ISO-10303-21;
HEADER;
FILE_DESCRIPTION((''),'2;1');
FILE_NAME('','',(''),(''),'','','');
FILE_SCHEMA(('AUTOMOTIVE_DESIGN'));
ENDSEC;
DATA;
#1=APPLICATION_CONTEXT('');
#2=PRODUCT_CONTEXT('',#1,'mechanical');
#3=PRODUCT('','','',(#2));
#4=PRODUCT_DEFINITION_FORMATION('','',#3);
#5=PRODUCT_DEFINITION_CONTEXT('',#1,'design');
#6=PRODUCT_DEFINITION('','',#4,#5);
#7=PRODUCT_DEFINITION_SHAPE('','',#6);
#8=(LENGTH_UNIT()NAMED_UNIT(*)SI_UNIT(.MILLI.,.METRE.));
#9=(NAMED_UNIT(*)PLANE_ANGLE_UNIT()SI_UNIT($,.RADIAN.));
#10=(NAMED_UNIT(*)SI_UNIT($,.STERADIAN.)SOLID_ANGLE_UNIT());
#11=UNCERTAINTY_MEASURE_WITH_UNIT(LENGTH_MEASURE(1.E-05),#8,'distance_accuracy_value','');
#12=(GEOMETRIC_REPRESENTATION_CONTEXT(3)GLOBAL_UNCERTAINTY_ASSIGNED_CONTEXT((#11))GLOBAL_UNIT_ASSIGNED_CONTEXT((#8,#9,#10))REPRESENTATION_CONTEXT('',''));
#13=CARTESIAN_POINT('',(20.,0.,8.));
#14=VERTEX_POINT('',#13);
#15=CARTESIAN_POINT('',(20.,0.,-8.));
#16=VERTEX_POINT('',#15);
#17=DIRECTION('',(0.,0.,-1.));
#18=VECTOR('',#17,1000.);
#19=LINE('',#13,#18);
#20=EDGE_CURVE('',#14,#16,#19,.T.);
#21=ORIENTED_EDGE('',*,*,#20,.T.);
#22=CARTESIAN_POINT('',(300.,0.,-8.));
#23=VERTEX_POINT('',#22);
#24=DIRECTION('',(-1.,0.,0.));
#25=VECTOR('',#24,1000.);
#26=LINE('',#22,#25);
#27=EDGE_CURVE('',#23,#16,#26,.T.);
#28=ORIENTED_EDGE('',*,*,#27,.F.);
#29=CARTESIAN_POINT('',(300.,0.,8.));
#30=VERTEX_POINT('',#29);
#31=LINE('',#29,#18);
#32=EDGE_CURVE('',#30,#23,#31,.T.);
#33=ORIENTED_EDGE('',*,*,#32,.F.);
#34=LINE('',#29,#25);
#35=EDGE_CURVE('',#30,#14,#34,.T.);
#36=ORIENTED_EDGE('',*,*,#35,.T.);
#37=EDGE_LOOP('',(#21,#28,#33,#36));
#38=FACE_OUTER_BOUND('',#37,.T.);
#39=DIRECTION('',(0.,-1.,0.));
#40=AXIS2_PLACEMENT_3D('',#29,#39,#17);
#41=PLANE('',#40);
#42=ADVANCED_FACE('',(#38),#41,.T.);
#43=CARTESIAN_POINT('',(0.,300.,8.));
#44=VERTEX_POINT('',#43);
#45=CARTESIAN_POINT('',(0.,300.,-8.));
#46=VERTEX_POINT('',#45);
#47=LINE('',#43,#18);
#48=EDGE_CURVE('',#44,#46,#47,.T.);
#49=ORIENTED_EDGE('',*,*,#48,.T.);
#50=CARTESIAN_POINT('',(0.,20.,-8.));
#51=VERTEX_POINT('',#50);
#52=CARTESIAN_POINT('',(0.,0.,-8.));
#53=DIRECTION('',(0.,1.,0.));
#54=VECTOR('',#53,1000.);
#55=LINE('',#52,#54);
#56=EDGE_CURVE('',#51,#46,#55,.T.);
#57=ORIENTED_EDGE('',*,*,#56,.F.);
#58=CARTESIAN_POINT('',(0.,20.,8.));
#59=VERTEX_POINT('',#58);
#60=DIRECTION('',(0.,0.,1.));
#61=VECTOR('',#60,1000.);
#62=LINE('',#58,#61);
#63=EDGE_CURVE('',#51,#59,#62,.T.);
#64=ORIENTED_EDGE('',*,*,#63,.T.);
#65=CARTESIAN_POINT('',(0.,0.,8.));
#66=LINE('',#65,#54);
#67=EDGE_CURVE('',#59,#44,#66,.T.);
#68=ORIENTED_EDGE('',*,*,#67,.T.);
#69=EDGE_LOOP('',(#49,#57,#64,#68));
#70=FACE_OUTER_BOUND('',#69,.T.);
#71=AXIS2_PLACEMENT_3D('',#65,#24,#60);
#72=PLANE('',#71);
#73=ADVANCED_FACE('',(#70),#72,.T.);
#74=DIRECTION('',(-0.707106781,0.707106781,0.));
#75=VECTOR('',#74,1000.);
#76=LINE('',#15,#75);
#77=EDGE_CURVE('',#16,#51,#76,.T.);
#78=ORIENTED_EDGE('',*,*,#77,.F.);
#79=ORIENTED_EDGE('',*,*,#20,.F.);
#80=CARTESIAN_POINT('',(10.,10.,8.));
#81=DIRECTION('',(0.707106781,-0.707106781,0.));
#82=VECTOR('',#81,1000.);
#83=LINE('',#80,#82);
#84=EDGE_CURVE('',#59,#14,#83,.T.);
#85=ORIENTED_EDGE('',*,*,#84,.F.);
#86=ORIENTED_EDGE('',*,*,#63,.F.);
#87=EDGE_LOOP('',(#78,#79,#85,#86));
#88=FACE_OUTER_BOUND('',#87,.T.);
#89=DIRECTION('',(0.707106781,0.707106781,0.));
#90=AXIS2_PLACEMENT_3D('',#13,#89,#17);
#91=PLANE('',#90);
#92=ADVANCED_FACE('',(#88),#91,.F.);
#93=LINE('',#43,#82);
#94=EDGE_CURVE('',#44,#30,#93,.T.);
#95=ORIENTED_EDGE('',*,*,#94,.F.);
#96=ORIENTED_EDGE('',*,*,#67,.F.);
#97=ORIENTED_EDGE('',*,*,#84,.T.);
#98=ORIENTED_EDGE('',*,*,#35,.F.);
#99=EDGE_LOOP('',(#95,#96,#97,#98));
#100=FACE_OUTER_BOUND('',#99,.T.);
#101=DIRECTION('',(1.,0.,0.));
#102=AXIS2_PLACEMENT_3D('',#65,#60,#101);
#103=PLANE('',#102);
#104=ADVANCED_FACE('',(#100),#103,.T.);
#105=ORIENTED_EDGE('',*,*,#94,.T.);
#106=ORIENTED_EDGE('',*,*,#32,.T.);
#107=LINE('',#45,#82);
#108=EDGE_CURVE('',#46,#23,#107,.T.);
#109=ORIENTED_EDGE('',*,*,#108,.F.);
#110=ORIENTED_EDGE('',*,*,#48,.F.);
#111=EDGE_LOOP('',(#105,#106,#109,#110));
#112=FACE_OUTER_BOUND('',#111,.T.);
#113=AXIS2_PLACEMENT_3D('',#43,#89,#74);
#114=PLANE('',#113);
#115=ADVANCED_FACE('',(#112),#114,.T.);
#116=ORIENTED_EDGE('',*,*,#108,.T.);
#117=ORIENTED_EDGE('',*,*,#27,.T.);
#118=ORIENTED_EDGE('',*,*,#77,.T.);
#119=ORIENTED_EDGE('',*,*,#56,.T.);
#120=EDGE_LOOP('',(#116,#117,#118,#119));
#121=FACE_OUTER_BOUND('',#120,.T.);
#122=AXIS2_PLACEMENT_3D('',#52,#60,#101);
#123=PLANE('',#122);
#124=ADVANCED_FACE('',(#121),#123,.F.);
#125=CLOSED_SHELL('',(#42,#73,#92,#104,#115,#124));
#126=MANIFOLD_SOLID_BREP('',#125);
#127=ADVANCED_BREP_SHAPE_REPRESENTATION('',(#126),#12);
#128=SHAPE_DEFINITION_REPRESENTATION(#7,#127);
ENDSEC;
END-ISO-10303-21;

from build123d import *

# Parameters (mm, degrees)
BOSS_EXTRUDE1_DEPTH = 8
CHAMFER1_SIZE       = 20


with BuildPart() as part:
    # Sketch1 → Boss-Extrude1 (new, symmetric)
    with BuildSketch(Plane.XY):
        Polygon((0, 0), (0, 300), (300, 0), align=None)
    extrude(amount=BOSS_EXTRUDE1_DEPTH, both=True)

    # Chamfer1
    chamfer1_edges = [part.edges().sort_by_distance(p)[0] for p in [
        (0, 0, 0),
    ]]
    chamfer(chamfer1_edges, length=CHAMFER1_SIZE)


solid = part.part
